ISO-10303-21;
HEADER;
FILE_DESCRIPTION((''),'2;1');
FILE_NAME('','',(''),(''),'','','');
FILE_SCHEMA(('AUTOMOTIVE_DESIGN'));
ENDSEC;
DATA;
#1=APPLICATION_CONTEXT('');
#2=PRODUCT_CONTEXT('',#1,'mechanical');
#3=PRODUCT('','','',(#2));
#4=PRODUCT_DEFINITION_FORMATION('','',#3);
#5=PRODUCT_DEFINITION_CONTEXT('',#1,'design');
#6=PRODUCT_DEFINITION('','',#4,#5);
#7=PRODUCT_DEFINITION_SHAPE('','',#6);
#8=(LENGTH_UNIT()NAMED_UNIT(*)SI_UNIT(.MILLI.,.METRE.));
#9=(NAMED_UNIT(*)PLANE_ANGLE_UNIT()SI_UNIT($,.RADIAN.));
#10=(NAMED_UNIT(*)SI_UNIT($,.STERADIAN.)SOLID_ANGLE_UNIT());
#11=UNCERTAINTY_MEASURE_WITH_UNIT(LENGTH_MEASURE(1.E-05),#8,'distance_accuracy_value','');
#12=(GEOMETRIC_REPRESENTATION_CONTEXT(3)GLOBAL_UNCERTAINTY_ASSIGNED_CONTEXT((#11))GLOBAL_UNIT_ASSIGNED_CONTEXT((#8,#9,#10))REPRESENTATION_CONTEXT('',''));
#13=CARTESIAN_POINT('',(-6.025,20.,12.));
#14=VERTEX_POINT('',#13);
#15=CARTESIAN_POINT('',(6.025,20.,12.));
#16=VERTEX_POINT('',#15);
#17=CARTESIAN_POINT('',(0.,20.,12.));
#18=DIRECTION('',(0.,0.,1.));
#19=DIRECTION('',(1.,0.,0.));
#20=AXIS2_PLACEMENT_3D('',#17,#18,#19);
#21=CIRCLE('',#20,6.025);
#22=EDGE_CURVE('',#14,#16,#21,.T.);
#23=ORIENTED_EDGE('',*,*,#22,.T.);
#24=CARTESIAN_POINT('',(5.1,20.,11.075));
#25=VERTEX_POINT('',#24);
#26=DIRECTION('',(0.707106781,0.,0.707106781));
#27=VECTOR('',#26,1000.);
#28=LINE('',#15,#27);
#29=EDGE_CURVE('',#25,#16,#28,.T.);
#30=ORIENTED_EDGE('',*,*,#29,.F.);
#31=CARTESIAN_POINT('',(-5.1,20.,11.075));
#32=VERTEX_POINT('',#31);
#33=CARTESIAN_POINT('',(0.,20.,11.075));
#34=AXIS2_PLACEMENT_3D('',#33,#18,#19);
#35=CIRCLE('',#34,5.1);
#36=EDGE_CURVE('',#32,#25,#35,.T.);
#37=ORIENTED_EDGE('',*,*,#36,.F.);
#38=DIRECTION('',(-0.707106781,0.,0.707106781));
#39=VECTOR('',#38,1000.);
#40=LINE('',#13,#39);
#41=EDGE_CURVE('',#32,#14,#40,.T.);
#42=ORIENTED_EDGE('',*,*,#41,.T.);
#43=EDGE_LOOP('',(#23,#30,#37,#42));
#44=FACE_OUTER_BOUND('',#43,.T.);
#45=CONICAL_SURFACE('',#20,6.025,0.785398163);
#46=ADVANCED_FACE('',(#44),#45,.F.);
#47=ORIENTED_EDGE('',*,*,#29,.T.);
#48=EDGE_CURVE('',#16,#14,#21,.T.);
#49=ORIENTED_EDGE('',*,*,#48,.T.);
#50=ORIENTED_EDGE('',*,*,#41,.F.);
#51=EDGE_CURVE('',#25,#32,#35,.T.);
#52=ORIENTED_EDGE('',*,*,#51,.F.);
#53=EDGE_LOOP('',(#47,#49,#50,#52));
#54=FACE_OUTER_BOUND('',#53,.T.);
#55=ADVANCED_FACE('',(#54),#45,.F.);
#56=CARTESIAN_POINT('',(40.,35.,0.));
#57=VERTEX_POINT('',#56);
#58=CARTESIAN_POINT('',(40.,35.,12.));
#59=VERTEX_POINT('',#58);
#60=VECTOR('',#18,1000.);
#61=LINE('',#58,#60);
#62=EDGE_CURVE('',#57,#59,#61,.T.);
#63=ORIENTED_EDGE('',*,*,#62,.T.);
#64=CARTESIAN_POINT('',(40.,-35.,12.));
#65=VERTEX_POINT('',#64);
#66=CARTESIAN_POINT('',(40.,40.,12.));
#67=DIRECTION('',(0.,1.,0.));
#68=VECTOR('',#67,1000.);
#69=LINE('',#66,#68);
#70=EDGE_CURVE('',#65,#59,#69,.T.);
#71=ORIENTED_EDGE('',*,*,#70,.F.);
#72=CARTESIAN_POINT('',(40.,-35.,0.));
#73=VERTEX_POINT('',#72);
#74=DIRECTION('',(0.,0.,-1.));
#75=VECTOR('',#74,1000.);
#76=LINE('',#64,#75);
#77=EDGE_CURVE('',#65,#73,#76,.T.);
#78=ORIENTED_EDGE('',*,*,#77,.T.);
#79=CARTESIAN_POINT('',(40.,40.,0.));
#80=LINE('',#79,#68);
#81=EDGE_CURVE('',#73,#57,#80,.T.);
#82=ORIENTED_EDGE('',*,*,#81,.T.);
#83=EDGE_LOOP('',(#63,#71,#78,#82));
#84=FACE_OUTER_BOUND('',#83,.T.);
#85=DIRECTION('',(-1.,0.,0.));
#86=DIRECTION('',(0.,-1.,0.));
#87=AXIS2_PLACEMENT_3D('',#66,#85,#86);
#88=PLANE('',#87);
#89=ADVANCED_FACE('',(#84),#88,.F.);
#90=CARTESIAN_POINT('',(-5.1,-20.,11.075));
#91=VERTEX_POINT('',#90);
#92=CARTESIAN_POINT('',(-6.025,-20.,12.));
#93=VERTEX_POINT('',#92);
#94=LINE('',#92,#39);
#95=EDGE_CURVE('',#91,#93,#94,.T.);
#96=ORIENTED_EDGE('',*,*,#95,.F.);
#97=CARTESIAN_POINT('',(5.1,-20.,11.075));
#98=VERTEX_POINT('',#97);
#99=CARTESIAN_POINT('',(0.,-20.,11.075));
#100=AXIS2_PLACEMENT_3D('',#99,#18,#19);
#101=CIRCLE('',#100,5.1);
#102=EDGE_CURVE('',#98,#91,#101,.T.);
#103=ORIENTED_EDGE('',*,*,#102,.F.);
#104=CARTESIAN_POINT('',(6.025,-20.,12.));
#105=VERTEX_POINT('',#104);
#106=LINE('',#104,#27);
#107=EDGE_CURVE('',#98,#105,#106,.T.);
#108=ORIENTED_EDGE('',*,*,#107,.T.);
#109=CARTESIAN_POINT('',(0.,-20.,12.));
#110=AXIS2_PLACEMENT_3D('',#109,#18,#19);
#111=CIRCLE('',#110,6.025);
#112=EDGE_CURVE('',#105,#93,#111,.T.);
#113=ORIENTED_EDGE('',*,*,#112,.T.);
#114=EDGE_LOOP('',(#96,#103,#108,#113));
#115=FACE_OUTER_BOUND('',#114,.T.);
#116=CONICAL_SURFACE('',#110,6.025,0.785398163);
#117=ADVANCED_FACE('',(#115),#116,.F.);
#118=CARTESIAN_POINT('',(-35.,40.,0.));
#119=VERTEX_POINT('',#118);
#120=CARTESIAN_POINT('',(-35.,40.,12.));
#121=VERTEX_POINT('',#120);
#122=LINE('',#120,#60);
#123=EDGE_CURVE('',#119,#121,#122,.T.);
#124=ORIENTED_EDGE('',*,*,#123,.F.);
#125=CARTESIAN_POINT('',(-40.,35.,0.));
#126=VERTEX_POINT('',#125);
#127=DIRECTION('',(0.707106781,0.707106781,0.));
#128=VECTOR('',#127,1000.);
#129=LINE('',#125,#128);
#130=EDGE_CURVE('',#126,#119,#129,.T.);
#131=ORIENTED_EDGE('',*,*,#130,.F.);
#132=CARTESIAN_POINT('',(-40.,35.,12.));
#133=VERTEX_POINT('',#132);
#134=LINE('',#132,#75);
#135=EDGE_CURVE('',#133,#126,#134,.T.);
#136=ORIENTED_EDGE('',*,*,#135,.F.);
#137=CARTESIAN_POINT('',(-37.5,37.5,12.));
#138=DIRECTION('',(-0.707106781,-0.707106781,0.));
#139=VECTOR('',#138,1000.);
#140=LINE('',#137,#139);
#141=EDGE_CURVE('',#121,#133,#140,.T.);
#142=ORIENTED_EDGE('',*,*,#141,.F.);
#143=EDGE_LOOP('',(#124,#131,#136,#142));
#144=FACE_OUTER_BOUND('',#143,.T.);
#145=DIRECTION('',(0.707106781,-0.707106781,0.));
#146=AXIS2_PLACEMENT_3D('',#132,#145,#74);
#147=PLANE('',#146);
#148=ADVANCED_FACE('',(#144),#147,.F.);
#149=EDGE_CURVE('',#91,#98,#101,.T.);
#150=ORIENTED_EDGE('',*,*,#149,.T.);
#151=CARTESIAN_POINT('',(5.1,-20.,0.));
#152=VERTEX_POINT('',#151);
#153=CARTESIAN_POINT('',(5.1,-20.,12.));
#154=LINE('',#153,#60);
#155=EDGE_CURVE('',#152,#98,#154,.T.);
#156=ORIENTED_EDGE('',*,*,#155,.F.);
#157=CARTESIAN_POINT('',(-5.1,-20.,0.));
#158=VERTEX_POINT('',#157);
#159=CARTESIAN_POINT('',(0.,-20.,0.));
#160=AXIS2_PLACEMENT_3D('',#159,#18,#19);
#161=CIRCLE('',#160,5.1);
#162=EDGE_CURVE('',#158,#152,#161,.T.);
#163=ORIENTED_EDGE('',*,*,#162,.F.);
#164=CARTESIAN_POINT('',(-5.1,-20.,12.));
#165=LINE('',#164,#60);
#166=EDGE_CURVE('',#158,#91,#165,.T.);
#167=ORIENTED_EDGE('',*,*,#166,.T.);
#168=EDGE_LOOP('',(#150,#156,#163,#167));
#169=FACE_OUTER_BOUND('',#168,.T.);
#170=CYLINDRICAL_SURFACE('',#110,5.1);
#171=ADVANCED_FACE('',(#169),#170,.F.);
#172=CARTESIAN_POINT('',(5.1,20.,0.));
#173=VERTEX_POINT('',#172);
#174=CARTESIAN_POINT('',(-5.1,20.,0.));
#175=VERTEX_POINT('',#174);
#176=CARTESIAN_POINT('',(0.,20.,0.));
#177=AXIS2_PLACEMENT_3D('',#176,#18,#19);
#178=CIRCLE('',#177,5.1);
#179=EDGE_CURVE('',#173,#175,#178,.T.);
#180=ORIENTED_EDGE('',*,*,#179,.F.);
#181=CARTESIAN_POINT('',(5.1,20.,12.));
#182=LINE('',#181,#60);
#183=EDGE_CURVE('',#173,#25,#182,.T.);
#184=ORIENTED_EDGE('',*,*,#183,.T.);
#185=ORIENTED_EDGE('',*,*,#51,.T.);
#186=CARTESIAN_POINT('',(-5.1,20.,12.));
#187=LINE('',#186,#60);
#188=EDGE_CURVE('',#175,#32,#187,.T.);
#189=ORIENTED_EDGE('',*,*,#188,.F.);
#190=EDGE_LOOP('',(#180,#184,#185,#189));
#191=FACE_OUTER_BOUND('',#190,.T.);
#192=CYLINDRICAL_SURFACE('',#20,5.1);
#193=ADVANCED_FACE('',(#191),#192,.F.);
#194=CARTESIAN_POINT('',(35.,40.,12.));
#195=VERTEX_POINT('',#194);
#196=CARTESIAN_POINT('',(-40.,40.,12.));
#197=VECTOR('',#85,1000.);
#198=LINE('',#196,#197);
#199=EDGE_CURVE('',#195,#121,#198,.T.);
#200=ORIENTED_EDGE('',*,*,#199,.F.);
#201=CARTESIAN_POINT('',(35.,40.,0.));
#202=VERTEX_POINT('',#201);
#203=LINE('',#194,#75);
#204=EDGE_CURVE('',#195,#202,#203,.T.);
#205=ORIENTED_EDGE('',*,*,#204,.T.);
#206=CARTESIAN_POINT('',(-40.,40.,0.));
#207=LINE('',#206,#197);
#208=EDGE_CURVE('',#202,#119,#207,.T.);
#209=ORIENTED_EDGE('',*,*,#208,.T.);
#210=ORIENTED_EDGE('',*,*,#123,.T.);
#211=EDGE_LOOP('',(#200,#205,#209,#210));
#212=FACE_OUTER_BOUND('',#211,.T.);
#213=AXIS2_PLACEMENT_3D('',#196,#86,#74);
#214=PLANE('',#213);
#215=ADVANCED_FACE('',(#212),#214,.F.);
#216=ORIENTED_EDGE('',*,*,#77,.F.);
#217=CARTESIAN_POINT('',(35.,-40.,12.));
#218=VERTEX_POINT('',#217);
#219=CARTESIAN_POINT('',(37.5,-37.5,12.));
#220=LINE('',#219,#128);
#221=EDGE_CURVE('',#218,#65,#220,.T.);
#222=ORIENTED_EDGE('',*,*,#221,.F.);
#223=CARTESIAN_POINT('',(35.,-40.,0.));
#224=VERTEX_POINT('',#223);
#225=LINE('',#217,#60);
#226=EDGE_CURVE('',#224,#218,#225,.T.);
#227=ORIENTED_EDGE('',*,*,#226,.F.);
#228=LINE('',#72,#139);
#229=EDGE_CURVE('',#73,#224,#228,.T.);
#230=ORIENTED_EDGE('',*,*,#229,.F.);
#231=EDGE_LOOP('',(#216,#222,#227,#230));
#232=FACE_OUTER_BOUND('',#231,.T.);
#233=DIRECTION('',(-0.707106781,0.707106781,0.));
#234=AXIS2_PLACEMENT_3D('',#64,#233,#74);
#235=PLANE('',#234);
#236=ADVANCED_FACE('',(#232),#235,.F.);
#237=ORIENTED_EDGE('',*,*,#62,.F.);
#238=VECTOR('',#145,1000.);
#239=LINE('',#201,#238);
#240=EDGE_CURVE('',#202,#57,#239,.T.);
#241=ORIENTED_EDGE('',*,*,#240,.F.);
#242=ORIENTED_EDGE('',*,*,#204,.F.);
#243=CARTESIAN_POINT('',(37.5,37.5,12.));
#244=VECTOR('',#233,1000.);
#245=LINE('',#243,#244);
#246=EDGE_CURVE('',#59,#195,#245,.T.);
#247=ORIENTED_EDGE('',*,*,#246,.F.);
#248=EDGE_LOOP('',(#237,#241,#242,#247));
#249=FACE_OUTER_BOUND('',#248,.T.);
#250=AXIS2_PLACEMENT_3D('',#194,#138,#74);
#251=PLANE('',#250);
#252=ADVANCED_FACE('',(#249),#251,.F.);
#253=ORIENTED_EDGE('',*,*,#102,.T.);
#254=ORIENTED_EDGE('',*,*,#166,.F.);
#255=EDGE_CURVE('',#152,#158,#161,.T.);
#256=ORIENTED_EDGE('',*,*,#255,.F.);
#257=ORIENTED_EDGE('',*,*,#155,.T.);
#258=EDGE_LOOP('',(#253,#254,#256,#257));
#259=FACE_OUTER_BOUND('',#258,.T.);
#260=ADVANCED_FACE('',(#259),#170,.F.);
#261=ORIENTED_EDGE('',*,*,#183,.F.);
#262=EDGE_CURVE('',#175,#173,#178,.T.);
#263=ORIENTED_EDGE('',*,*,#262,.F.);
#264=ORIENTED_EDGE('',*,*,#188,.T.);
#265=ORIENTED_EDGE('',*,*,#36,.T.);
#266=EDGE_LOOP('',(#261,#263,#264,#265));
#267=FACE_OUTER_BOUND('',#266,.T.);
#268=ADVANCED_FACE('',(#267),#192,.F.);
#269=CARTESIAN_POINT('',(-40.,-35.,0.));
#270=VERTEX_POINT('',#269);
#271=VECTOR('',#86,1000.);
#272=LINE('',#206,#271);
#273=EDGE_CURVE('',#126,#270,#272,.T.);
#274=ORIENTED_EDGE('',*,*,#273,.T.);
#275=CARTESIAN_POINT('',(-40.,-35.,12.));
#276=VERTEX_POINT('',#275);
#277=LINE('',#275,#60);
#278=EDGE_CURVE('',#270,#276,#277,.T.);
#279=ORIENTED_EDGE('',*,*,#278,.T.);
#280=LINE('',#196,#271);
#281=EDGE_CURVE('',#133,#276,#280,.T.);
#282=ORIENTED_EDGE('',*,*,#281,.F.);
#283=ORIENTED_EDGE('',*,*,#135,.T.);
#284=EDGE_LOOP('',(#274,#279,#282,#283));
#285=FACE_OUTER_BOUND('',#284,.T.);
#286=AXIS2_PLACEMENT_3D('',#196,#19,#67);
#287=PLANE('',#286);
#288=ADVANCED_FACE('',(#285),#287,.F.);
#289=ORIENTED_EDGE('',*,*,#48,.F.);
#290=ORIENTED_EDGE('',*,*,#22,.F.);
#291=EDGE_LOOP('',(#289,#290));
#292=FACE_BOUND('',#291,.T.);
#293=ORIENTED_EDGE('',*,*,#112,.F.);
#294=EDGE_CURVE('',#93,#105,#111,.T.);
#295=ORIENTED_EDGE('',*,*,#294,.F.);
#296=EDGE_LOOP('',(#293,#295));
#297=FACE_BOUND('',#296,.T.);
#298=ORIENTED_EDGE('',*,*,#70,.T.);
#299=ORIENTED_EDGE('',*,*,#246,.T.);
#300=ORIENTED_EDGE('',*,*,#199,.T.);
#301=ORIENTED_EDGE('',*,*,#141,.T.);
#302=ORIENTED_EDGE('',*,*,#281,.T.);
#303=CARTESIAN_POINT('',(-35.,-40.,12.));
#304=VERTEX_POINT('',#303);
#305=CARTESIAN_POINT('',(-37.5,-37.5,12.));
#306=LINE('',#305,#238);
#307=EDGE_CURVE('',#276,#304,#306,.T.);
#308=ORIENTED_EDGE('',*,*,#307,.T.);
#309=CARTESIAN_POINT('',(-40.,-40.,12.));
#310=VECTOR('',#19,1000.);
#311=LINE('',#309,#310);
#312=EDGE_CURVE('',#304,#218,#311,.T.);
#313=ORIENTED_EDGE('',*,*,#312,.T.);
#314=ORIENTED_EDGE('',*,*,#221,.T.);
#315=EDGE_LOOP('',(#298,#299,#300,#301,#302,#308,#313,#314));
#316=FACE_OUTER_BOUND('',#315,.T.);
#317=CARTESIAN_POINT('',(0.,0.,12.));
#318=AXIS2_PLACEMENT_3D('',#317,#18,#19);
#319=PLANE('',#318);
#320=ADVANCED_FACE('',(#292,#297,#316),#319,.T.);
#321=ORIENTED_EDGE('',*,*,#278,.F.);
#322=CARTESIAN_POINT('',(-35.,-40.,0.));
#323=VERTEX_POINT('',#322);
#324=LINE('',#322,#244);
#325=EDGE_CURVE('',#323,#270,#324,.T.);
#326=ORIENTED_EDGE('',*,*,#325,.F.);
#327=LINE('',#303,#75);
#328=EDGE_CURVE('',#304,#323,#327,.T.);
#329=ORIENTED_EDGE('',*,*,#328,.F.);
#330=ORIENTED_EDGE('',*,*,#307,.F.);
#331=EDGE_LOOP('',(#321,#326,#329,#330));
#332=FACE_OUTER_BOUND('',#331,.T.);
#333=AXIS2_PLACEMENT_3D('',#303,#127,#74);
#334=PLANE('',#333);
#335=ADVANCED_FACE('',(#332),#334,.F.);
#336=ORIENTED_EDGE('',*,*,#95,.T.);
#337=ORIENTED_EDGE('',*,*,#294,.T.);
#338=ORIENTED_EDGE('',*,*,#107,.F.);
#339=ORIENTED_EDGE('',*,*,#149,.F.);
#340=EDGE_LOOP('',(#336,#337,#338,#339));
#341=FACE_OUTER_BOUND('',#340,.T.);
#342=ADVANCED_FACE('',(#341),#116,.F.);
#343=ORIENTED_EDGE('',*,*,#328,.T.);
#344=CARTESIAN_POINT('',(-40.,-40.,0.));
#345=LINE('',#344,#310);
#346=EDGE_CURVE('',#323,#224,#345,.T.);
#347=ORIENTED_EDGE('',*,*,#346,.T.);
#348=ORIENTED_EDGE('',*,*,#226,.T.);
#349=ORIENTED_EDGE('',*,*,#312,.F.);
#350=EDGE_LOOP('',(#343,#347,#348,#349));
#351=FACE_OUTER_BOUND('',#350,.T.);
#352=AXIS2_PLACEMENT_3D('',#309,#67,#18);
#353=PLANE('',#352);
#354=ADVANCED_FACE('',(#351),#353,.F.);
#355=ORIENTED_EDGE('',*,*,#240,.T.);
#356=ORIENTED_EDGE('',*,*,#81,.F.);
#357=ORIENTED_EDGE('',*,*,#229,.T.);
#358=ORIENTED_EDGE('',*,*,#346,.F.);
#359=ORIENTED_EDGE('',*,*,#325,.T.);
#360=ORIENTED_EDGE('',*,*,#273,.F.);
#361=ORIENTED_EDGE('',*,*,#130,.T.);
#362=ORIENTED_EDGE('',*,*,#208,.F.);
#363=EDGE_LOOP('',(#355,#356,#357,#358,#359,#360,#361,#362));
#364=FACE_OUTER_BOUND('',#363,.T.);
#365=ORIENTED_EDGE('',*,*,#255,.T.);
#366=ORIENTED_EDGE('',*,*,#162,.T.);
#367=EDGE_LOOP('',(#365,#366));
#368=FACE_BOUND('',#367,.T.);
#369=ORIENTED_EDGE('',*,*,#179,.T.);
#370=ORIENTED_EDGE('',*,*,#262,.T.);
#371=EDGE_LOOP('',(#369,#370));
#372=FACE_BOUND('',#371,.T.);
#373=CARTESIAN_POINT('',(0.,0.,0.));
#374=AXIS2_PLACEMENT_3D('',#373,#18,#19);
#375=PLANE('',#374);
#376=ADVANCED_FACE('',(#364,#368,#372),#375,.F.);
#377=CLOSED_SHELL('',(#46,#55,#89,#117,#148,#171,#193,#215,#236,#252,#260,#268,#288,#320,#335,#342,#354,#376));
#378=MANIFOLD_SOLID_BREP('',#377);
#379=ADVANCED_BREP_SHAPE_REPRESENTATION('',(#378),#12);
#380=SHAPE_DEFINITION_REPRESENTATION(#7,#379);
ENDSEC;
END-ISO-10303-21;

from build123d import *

# Parameters (mm, degrees)
SKETCH_1_W                    = 80
SKETCH_1_H                    = 80
EXTRUDE_1_DEPTH               = 12
CHAMFER_1_SIZE                = 5
HOLE_WIZARD_M12_1_D           = 10.2
HOLE_WIZARD_M12_1_DEPTH       = 32.75
HOLE_WIZARD_M12_1_CSINK_D     = 12.05
HOLE_WIZARD_M12_1_CSINK_ANGLE = 90
HOLE_WIZARD_M12_1_TIP         = 3.064389157


with BuildPart() as part:
    # 草图1 → 凸台-拉伸1 (new body)
    with BuildSketch(Plane.XY):
        Rectangle(SKETCH_1_W, SKETCH_1_H)
    extrude(amount=EXTRUDE_1_DEPTH)

    # 倒角1
    chamfer_1_edges = [part.edges().sort_by_distance(p)[0] for p in [
        (40, -40, 6),
        (-40, -40, 6),
        (-40, 40, 6),
        (40, 40, 6),
    ]]
    chamfer(chamfer_1_edges, length=CHAMFER_1_SIZE)

    # M12 螺纹孔1
    with Locations(Plane(origin=(0, 20, 12), x_dir=(1, 0, 0), z_dir=(0, 0, 1))):
        with Locations((0, 0), (0, -40)):
            CounterSinkHole(HOLE_WIZARD_M12_1_D / 2, HOLE_WIZARD_M12_1_CSINK_D / 2, depth=HOLE_WIZARD_M12_1_DEPTH, counter_sink_angle=HOLE_WIZARD_M12_1_CSINK_ANGLE)
            with Locations((0, 0, -(HOLE_WIZARD_M12_1_DEPTH + HOLE_WIZARD_M12_1_TIP / 2))):  # 118° drill point
                Cone(0, HOLE_WIZARD_M12_1_D / 2, HOLE_WIZARD_M12_1_TIP, mode=Mode.SUBTRACT)


solid = part.part
